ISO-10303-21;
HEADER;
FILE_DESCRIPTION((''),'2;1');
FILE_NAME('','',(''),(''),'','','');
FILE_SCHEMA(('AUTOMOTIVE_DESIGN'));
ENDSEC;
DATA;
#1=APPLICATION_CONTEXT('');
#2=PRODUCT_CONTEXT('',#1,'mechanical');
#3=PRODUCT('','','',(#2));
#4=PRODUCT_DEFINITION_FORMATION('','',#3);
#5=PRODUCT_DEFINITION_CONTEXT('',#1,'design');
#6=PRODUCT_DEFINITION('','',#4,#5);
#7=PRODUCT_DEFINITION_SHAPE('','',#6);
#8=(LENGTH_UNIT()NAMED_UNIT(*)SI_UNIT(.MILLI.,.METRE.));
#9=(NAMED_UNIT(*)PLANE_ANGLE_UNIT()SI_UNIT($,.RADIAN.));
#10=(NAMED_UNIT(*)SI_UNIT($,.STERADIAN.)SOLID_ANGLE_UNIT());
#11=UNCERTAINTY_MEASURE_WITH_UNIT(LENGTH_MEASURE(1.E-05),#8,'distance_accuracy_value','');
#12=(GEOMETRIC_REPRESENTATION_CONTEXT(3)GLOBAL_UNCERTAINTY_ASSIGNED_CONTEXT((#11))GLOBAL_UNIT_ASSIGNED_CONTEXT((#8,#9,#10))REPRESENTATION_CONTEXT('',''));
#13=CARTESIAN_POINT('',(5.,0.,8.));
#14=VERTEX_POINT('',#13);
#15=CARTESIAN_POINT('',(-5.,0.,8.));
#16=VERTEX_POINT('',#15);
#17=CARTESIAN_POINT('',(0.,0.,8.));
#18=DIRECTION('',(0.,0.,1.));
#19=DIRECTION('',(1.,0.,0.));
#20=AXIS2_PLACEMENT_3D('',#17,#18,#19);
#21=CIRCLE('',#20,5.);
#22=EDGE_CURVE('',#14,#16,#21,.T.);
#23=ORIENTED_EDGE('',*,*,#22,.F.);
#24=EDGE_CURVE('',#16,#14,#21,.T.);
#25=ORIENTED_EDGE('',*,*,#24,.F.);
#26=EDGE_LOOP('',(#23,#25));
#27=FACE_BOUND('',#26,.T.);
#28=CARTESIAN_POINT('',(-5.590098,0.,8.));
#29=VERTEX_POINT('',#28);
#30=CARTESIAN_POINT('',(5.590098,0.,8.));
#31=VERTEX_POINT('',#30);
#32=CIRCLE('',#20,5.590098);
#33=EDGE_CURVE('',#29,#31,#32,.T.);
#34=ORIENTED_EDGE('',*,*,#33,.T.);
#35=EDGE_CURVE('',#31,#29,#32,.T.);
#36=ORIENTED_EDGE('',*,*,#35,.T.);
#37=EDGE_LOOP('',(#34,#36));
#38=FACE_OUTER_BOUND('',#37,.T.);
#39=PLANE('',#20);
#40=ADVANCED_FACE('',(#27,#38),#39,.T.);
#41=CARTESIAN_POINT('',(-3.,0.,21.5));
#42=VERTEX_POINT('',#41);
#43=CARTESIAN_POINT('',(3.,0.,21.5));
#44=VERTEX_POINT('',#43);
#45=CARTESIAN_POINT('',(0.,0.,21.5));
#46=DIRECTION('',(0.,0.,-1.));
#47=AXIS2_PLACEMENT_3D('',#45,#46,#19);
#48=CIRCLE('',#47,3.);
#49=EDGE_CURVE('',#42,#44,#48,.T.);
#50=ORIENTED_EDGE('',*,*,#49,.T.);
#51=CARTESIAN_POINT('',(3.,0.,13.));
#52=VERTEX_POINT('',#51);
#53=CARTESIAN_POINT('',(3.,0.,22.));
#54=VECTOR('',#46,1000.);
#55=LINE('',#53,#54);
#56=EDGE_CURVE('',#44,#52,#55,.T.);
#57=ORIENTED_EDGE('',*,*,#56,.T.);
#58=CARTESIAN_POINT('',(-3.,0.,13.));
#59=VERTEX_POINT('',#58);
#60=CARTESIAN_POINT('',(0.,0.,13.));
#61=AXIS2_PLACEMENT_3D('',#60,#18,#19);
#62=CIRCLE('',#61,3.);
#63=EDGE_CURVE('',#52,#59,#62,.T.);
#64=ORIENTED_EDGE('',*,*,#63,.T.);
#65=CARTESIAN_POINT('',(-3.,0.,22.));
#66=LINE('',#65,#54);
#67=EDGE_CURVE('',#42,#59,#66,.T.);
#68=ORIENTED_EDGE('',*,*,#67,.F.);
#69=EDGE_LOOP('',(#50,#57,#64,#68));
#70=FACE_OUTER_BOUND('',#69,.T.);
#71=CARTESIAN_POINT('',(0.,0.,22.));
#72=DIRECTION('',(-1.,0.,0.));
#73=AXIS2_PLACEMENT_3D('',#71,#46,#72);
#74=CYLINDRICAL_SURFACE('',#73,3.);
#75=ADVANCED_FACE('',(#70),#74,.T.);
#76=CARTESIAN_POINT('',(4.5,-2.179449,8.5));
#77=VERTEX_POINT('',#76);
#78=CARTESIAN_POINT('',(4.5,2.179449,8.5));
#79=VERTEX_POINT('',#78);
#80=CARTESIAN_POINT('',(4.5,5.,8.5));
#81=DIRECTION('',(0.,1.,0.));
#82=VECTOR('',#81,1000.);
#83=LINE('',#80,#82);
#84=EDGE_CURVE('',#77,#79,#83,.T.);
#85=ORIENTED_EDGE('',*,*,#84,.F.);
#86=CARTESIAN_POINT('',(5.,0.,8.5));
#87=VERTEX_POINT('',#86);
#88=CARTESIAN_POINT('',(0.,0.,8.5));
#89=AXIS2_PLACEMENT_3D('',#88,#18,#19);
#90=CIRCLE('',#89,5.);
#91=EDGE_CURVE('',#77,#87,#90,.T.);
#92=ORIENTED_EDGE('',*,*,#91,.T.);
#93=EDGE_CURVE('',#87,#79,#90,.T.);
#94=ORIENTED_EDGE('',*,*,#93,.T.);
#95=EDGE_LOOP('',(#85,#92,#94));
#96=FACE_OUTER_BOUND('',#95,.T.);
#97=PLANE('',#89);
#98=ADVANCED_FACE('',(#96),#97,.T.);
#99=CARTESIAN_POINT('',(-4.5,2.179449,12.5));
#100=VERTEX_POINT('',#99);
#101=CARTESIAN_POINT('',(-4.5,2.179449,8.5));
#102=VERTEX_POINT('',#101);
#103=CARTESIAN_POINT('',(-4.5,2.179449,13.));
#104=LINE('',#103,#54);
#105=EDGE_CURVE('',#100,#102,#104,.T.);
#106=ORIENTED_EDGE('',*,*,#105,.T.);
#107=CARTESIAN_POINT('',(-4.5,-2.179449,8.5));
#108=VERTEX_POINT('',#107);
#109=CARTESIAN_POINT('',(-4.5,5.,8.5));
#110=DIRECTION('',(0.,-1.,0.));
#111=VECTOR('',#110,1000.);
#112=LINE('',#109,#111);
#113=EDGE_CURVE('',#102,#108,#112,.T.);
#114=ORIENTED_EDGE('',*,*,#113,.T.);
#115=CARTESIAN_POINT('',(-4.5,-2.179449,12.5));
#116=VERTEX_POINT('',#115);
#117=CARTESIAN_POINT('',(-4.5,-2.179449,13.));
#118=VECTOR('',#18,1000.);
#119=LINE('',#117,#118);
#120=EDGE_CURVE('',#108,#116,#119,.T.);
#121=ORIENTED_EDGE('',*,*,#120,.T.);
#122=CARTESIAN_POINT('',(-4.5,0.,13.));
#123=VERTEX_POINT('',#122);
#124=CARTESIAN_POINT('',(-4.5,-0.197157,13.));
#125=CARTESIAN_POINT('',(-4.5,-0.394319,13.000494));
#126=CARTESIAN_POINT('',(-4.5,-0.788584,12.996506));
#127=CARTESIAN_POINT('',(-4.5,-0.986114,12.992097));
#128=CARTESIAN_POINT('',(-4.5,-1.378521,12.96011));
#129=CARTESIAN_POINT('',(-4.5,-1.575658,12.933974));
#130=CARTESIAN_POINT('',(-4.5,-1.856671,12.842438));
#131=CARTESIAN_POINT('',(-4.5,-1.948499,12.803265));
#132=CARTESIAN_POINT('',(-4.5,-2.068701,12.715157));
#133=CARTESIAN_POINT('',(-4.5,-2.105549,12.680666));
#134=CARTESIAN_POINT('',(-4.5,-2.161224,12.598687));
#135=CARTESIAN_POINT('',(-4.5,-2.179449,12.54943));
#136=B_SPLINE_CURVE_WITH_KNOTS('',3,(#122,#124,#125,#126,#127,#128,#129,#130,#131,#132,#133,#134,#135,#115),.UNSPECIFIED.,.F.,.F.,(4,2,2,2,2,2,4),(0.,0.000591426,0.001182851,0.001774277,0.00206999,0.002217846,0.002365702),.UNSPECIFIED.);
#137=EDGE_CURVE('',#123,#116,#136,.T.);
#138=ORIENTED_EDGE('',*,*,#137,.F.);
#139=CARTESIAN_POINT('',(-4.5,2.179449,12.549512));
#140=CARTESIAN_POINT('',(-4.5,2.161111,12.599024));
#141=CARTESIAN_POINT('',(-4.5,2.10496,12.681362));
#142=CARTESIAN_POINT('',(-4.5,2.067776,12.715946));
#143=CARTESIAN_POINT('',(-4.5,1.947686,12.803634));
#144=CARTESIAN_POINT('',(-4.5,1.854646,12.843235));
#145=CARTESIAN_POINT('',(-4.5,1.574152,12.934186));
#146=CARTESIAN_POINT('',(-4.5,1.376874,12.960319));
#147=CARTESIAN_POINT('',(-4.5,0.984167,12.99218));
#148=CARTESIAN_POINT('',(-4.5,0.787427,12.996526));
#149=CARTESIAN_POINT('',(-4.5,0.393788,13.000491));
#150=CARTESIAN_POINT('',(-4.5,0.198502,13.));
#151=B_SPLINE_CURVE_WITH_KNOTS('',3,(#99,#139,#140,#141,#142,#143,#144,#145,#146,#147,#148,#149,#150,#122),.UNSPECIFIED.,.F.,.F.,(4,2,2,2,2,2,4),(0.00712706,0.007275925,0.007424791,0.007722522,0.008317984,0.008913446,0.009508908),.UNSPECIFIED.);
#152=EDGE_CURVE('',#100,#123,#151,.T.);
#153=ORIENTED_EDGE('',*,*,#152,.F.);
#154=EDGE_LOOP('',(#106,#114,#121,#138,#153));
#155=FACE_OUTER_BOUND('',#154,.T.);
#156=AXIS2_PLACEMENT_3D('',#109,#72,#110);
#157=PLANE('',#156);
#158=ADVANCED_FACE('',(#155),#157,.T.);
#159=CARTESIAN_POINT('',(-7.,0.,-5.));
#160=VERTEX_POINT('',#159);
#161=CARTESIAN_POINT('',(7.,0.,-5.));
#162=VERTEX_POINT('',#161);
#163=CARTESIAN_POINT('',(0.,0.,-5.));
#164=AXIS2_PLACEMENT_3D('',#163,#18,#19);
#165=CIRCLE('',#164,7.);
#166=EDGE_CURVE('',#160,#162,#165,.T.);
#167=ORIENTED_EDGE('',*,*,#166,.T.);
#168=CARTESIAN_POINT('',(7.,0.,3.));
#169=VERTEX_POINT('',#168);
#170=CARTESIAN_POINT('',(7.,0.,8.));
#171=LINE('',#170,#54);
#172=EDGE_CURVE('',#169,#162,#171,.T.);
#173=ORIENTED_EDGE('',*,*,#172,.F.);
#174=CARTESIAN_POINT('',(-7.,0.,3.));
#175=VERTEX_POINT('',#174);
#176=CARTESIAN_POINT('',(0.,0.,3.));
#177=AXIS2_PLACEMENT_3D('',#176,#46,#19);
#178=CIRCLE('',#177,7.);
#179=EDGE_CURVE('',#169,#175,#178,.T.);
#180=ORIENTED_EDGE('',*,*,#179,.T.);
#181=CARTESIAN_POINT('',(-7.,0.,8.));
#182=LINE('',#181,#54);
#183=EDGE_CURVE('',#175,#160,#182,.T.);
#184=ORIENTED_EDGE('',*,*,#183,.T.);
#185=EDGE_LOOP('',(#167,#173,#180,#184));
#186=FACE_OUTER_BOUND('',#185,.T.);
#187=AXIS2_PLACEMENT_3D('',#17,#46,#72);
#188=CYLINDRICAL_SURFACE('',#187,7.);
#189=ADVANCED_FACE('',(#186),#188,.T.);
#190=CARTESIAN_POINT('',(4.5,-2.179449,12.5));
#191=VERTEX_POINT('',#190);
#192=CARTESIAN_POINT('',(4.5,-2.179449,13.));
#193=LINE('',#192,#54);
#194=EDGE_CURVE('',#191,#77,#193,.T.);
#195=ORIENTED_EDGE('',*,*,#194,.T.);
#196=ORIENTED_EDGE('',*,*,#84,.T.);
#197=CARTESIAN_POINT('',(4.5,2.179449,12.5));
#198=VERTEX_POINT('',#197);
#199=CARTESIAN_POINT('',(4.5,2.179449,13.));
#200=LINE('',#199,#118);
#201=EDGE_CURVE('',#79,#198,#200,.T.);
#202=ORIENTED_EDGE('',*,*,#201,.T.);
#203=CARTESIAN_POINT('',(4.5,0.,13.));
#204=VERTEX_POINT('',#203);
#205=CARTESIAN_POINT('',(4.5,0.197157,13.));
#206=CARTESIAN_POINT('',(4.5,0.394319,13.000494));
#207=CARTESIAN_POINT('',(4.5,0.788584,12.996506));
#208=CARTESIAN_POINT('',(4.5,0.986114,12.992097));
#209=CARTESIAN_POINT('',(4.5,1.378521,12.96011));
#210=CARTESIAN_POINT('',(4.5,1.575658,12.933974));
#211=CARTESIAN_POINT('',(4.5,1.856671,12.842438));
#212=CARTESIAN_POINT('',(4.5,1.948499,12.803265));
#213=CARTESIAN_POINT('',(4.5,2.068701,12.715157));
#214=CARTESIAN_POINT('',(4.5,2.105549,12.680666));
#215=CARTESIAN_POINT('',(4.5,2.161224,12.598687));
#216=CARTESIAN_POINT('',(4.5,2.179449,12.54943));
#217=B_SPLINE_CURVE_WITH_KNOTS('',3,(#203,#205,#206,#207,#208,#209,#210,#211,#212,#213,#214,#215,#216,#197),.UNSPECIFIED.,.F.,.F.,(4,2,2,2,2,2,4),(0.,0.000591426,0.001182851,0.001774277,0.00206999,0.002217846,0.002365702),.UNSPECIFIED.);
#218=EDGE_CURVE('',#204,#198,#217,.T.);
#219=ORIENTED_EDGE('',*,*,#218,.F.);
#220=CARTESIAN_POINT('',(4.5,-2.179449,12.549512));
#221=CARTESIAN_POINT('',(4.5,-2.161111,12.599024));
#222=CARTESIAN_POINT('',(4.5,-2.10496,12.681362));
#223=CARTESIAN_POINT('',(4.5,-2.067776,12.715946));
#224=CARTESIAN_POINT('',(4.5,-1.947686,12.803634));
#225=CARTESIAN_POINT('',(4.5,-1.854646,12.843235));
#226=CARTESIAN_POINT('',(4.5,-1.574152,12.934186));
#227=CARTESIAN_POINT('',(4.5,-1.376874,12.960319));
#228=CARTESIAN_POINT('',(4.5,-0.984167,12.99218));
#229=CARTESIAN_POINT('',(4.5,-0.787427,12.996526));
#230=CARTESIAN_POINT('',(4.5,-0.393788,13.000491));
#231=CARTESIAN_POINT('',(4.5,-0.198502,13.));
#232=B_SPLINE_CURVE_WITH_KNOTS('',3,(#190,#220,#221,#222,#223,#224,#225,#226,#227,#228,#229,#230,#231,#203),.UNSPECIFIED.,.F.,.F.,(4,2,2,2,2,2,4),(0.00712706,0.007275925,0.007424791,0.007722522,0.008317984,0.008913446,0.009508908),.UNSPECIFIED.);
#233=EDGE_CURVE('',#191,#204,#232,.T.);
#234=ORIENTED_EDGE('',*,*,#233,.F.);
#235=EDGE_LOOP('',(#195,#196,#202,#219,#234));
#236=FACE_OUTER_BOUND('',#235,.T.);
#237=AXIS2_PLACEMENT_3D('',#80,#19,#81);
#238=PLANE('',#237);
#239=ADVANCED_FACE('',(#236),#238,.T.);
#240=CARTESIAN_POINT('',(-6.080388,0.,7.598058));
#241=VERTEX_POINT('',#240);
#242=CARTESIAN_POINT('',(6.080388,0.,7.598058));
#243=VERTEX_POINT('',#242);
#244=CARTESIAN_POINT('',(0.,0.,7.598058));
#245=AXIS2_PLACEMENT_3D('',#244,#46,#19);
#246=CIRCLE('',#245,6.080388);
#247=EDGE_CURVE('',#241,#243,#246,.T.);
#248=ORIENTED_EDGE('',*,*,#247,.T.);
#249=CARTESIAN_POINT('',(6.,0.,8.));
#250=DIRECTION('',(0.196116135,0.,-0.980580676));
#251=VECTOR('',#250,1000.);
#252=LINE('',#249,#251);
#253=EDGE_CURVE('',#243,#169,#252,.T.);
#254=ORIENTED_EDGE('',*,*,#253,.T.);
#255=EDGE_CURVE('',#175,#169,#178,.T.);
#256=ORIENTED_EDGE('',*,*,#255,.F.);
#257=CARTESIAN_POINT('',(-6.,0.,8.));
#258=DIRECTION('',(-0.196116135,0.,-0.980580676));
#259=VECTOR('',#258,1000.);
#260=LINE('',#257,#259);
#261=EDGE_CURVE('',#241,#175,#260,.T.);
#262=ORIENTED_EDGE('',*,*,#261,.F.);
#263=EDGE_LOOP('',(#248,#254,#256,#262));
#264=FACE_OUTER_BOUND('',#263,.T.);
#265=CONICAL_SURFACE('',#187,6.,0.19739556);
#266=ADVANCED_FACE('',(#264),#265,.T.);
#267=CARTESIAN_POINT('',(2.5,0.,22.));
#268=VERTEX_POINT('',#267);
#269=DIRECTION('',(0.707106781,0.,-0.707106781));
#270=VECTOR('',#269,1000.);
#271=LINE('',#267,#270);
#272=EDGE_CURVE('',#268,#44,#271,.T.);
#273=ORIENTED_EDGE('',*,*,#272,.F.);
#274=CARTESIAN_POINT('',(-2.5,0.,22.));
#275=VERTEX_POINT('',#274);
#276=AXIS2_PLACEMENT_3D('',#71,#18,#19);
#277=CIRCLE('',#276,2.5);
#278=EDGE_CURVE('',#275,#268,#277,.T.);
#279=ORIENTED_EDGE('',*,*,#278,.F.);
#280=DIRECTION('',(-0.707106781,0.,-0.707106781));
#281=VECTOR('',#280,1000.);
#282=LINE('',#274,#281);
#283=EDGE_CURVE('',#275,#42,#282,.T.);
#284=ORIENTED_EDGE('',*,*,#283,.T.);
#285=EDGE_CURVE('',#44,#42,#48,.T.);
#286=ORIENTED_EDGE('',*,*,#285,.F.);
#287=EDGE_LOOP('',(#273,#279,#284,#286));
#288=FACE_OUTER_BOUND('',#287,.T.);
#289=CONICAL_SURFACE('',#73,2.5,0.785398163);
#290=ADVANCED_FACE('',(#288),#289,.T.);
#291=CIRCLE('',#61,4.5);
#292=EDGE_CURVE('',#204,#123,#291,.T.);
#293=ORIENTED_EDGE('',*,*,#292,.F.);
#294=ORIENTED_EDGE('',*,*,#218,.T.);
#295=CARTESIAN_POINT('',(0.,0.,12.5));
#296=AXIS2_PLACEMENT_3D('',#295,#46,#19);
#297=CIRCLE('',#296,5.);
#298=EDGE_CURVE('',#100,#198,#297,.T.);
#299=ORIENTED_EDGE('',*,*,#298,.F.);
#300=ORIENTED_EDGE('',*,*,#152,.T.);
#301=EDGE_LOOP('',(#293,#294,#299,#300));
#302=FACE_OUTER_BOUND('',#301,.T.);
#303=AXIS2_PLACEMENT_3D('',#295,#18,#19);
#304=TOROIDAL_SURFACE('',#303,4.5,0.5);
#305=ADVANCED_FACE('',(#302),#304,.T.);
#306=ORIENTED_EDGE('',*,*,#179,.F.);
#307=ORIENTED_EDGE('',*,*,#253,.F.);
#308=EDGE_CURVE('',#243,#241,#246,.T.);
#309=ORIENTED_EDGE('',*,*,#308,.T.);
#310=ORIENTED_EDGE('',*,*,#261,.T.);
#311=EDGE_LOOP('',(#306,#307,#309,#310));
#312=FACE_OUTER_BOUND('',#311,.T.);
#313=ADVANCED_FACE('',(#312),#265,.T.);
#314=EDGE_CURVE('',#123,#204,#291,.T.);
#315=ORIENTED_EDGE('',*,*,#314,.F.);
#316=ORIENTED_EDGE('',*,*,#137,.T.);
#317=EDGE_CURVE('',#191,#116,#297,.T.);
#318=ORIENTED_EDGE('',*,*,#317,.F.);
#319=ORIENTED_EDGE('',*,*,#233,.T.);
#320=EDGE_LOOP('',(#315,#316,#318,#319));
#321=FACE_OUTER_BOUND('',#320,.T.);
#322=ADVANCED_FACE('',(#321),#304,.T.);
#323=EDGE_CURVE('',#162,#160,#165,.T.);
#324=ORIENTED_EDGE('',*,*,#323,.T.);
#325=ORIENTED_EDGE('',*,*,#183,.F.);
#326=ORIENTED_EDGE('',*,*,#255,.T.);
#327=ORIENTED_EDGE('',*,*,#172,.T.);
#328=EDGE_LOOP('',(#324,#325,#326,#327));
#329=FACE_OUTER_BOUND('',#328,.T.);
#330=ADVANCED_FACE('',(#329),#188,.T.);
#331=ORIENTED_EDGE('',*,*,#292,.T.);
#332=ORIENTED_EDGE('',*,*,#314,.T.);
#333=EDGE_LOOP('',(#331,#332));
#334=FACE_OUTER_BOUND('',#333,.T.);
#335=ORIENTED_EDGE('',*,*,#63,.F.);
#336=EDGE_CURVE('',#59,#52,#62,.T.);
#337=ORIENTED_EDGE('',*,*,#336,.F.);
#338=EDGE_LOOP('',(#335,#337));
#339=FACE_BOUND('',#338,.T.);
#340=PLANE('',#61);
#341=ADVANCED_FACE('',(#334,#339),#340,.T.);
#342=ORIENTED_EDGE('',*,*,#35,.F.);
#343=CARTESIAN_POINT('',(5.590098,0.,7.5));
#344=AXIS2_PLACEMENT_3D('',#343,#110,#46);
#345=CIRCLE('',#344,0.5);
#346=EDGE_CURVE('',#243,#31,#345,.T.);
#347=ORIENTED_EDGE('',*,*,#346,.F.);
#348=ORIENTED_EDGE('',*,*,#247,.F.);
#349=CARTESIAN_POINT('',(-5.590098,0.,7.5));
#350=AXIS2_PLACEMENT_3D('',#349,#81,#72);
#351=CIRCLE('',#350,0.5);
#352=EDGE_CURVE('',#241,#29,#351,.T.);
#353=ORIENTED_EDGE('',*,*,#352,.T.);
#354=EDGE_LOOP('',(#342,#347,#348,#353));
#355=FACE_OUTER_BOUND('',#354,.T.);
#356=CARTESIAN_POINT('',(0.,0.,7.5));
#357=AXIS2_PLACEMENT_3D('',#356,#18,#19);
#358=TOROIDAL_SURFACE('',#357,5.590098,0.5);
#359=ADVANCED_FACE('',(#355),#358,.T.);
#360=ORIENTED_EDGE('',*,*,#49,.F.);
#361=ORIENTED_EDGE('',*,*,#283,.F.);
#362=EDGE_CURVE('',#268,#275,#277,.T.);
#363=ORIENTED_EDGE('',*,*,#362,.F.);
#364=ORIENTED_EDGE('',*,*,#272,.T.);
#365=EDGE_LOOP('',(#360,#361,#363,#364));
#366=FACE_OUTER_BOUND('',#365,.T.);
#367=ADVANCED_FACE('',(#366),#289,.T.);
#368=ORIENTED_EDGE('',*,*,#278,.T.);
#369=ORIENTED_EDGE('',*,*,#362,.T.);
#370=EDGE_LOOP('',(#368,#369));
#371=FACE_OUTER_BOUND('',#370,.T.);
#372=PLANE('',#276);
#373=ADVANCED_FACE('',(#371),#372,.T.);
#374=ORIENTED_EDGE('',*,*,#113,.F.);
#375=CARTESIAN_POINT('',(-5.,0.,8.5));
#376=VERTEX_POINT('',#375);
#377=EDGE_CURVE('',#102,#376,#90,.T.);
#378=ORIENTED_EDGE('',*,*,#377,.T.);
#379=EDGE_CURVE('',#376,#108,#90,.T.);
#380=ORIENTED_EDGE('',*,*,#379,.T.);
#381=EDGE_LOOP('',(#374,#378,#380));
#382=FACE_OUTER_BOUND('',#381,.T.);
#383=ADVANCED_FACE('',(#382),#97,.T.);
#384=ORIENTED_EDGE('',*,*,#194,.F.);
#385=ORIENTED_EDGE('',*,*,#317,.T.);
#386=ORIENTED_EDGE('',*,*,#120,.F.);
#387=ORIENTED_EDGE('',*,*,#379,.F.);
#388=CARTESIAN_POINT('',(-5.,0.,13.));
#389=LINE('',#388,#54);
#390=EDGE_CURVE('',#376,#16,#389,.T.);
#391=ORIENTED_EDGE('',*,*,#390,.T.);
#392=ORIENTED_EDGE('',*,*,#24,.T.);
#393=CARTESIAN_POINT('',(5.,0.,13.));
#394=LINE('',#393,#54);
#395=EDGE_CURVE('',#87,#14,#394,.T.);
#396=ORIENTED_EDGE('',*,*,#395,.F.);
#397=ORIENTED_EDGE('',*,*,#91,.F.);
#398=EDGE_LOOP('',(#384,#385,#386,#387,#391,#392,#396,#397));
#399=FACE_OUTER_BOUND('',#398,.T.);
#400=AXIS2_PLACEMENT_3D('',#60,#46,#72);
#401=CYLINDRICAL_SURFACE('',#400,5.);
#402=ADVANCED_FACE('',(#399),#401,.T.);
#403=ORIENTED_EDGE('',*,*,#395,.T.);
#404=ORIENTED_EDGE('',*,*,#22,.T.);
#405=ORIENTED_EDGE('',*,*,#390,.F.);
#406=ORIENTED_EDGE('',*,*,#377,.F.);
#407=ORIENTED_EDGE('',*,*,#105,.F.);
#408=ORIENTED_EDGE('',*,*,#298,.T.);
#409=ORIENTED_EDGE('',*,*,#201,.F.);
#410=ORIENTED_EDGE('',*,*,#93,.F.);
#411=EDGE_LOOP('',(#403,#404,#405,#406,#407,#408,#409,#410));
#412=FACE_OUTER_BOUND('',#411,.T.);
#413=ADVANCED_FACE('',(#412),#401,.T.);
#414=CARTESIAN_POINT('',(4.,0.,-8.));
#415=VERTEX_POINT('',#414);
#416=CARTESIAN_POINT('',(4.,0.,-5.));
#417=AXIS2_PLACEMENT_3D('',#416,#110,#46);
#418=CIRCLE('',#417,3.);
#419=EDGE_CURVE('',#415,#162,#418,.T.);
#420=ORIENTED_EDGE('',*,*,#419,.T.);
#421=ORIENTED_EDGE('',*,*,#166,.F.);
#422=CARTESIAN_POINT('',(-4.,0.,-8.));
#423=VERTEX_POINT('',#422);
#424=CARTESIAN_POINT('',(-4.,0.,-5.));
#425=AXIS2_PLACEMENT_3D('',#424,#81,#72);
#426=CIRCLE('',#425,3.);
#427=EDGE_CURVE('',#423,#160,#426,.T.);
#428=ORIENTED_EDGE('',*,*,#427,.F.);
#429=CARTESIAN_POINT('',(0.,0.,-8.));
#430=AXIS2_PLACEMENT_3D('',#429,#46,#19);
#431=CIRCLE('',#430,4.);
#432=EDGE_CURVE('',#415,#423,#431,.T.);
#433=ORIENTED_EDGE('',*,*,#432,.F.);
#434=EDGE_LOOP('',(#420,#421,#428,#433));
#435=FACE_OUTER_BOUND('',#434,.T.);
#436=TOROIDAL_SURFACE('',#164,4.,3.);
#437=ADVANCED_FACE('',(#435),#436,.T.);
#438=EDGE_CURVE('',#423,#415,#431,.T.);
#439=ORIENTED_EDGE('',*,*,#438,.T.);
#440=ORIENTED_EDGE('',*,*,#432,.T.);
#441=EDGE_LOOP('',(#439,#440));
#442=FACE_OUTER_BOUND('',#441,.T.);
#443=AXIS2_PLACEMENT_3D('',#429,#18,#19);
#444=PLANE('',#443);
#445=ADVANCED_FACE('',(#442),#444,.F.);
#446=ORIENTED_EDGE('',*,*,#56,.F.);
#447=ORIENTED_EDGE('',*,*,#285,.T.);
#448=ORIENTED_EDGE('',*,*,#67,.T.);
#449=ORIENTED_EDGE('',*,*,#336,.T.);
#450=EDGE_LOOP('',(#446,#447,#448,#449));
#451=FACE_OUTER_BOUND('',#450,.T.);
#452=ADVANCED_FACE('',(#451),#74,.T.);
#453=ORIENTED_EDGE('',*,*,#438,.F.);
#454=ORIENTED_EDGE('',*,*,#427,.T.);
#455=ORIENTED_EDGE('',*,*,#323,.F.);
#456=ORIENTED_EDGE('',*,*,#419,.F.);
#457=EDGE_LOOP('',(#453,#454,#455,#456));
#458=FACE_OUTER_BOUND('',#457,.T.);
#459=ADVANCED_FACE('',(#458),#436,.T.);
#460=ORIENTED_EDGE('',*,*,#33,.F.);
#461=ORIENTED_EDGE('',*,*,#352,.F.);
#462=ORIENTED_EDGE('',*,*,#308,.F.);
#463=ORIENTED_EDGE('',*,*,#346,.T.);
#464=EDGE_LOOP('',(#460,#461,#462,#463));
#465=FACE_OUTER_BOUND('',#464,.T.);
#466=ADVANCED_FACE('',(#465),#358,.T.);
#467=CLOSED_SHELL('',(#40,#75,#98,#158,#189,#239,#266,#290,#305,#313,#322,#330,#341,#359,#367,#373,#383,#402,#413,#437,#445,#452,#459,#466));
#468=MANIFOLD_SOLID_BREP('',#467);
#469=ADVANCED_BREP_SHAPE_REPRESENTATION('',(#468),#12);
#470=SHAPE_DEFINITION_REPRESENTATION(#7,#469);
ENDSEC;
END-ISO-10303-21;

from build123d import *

# Parameters (mm, degrees)
SKETCH1_R           = 7
BOSS_EXTRUDE1_DEPTH = 8
SKETCH2_R           = 5
BOSS_EXTRUDE2_DEPTH = 5
SKETCH3_R           = 3
BOSS_EXTRUDE3_DEPTH = 9
CHAMFER1_SIZE       = 5
CHAMFER1_SIZE2      = 1
FILLET1_R           = 3
FILLET2_R           = 0.5
FILLET3_R           = 0.5
SKETCH4_OUTSIDE_W   = 23.188
SKETCH4_OUTSIDE_H   = 23.188
SKETCH4_OUTSIDE_W_2 = 9
SKETCH4_OUTSIDE_H_2 = 10
CUT_EXTRUDE1_DEPTH  = 4.5
CHAMFER3_SIZE       = 0.5


with BuildPart() as part:
    # Sketch1 → Boss-Extrude1 (new, symmetric)
    with BuildSketch(Plane.XY):
        Circle(SKETCH1_R)
    extrude(amount=BOSS_EXTRUDE1_DEPTH, both=True)

    # Sketch2 → Boss-Extrude2 (add)
    with BuildSketch(Plane.XY.offset(8)):
        Circle(SKETCH2_R)
    extrude(amount=BOSS_EXTRUDE2_DEPTH)

    # Sketch3 → Boss-Extrude3 (add)
    with BuildSketch(Plane.XY.offset(13)):
        Circle(SKETCH3_R)
    extrude(amount=BOSS_EXTRUDE3_DEPTH)

    # Chamfer1
    chamfer1_edges = [part.edges().sort_by_distance(p)[0] for p in [
        (-7, 0, 8),
    ]]
    chamfer1_side = [part.faces().sort_by_distance(p)[0] for p in [
        (-7, 0, 0),
    ]]
    chamfer(chamfer1_edges, length=CHAMFER1_SIZE, length2=CHAMFER1_SIZE2, reference=chamfer1_side[0])

    # Fillet1
    fillet1_edges = [part.edges().sort_by_distance(p)[0] for p in [
        (-7, 0, -8),
    ]]
    fillet(fillet1_edges, radius=FILLET1_R)

    # Fillet2
    fillet2_edges = [part.edges().sort_by_distance(p)[0] for p in [
        (-6, 0, 8),
    ]]
    fillet(fillet2_edges, radius=FILLET2_R)

    # Fillet3
    fillet3_edges = [part.edges().sort_by_distance(p)[0] for p in [
        (-5, 0, 13),
    ]]
    fillet(fillet3_edges, radius=FILLET3_R)

    # Sketch4 outside → Cut-Extrude1 (cut)
    with BuildSketch(Plane.XY.offset(13)):
        Rectangle(SKETCH4_OUTSIDE_W, SKETCH4_OUTSIDE_H)
        Rectangle(SKETCH4_OUTSIDE_W_2, SKETCH4_OUTSIDE_H_2, mode=Mode.SUBTRACT)
    extrude(amount=-CUT_EXTRUDE1_DEPTH, mode=Mode.SUBTRACT)

    # Chamfer3
    chamfer3_edges = [part.edges().sort_by_distance(p)[0] for p in [
        (-3, 0, 22),
    ]]
    chamfer(chamfer3_edges, length=CHAMFER3_SIZE)


solid = part.part
